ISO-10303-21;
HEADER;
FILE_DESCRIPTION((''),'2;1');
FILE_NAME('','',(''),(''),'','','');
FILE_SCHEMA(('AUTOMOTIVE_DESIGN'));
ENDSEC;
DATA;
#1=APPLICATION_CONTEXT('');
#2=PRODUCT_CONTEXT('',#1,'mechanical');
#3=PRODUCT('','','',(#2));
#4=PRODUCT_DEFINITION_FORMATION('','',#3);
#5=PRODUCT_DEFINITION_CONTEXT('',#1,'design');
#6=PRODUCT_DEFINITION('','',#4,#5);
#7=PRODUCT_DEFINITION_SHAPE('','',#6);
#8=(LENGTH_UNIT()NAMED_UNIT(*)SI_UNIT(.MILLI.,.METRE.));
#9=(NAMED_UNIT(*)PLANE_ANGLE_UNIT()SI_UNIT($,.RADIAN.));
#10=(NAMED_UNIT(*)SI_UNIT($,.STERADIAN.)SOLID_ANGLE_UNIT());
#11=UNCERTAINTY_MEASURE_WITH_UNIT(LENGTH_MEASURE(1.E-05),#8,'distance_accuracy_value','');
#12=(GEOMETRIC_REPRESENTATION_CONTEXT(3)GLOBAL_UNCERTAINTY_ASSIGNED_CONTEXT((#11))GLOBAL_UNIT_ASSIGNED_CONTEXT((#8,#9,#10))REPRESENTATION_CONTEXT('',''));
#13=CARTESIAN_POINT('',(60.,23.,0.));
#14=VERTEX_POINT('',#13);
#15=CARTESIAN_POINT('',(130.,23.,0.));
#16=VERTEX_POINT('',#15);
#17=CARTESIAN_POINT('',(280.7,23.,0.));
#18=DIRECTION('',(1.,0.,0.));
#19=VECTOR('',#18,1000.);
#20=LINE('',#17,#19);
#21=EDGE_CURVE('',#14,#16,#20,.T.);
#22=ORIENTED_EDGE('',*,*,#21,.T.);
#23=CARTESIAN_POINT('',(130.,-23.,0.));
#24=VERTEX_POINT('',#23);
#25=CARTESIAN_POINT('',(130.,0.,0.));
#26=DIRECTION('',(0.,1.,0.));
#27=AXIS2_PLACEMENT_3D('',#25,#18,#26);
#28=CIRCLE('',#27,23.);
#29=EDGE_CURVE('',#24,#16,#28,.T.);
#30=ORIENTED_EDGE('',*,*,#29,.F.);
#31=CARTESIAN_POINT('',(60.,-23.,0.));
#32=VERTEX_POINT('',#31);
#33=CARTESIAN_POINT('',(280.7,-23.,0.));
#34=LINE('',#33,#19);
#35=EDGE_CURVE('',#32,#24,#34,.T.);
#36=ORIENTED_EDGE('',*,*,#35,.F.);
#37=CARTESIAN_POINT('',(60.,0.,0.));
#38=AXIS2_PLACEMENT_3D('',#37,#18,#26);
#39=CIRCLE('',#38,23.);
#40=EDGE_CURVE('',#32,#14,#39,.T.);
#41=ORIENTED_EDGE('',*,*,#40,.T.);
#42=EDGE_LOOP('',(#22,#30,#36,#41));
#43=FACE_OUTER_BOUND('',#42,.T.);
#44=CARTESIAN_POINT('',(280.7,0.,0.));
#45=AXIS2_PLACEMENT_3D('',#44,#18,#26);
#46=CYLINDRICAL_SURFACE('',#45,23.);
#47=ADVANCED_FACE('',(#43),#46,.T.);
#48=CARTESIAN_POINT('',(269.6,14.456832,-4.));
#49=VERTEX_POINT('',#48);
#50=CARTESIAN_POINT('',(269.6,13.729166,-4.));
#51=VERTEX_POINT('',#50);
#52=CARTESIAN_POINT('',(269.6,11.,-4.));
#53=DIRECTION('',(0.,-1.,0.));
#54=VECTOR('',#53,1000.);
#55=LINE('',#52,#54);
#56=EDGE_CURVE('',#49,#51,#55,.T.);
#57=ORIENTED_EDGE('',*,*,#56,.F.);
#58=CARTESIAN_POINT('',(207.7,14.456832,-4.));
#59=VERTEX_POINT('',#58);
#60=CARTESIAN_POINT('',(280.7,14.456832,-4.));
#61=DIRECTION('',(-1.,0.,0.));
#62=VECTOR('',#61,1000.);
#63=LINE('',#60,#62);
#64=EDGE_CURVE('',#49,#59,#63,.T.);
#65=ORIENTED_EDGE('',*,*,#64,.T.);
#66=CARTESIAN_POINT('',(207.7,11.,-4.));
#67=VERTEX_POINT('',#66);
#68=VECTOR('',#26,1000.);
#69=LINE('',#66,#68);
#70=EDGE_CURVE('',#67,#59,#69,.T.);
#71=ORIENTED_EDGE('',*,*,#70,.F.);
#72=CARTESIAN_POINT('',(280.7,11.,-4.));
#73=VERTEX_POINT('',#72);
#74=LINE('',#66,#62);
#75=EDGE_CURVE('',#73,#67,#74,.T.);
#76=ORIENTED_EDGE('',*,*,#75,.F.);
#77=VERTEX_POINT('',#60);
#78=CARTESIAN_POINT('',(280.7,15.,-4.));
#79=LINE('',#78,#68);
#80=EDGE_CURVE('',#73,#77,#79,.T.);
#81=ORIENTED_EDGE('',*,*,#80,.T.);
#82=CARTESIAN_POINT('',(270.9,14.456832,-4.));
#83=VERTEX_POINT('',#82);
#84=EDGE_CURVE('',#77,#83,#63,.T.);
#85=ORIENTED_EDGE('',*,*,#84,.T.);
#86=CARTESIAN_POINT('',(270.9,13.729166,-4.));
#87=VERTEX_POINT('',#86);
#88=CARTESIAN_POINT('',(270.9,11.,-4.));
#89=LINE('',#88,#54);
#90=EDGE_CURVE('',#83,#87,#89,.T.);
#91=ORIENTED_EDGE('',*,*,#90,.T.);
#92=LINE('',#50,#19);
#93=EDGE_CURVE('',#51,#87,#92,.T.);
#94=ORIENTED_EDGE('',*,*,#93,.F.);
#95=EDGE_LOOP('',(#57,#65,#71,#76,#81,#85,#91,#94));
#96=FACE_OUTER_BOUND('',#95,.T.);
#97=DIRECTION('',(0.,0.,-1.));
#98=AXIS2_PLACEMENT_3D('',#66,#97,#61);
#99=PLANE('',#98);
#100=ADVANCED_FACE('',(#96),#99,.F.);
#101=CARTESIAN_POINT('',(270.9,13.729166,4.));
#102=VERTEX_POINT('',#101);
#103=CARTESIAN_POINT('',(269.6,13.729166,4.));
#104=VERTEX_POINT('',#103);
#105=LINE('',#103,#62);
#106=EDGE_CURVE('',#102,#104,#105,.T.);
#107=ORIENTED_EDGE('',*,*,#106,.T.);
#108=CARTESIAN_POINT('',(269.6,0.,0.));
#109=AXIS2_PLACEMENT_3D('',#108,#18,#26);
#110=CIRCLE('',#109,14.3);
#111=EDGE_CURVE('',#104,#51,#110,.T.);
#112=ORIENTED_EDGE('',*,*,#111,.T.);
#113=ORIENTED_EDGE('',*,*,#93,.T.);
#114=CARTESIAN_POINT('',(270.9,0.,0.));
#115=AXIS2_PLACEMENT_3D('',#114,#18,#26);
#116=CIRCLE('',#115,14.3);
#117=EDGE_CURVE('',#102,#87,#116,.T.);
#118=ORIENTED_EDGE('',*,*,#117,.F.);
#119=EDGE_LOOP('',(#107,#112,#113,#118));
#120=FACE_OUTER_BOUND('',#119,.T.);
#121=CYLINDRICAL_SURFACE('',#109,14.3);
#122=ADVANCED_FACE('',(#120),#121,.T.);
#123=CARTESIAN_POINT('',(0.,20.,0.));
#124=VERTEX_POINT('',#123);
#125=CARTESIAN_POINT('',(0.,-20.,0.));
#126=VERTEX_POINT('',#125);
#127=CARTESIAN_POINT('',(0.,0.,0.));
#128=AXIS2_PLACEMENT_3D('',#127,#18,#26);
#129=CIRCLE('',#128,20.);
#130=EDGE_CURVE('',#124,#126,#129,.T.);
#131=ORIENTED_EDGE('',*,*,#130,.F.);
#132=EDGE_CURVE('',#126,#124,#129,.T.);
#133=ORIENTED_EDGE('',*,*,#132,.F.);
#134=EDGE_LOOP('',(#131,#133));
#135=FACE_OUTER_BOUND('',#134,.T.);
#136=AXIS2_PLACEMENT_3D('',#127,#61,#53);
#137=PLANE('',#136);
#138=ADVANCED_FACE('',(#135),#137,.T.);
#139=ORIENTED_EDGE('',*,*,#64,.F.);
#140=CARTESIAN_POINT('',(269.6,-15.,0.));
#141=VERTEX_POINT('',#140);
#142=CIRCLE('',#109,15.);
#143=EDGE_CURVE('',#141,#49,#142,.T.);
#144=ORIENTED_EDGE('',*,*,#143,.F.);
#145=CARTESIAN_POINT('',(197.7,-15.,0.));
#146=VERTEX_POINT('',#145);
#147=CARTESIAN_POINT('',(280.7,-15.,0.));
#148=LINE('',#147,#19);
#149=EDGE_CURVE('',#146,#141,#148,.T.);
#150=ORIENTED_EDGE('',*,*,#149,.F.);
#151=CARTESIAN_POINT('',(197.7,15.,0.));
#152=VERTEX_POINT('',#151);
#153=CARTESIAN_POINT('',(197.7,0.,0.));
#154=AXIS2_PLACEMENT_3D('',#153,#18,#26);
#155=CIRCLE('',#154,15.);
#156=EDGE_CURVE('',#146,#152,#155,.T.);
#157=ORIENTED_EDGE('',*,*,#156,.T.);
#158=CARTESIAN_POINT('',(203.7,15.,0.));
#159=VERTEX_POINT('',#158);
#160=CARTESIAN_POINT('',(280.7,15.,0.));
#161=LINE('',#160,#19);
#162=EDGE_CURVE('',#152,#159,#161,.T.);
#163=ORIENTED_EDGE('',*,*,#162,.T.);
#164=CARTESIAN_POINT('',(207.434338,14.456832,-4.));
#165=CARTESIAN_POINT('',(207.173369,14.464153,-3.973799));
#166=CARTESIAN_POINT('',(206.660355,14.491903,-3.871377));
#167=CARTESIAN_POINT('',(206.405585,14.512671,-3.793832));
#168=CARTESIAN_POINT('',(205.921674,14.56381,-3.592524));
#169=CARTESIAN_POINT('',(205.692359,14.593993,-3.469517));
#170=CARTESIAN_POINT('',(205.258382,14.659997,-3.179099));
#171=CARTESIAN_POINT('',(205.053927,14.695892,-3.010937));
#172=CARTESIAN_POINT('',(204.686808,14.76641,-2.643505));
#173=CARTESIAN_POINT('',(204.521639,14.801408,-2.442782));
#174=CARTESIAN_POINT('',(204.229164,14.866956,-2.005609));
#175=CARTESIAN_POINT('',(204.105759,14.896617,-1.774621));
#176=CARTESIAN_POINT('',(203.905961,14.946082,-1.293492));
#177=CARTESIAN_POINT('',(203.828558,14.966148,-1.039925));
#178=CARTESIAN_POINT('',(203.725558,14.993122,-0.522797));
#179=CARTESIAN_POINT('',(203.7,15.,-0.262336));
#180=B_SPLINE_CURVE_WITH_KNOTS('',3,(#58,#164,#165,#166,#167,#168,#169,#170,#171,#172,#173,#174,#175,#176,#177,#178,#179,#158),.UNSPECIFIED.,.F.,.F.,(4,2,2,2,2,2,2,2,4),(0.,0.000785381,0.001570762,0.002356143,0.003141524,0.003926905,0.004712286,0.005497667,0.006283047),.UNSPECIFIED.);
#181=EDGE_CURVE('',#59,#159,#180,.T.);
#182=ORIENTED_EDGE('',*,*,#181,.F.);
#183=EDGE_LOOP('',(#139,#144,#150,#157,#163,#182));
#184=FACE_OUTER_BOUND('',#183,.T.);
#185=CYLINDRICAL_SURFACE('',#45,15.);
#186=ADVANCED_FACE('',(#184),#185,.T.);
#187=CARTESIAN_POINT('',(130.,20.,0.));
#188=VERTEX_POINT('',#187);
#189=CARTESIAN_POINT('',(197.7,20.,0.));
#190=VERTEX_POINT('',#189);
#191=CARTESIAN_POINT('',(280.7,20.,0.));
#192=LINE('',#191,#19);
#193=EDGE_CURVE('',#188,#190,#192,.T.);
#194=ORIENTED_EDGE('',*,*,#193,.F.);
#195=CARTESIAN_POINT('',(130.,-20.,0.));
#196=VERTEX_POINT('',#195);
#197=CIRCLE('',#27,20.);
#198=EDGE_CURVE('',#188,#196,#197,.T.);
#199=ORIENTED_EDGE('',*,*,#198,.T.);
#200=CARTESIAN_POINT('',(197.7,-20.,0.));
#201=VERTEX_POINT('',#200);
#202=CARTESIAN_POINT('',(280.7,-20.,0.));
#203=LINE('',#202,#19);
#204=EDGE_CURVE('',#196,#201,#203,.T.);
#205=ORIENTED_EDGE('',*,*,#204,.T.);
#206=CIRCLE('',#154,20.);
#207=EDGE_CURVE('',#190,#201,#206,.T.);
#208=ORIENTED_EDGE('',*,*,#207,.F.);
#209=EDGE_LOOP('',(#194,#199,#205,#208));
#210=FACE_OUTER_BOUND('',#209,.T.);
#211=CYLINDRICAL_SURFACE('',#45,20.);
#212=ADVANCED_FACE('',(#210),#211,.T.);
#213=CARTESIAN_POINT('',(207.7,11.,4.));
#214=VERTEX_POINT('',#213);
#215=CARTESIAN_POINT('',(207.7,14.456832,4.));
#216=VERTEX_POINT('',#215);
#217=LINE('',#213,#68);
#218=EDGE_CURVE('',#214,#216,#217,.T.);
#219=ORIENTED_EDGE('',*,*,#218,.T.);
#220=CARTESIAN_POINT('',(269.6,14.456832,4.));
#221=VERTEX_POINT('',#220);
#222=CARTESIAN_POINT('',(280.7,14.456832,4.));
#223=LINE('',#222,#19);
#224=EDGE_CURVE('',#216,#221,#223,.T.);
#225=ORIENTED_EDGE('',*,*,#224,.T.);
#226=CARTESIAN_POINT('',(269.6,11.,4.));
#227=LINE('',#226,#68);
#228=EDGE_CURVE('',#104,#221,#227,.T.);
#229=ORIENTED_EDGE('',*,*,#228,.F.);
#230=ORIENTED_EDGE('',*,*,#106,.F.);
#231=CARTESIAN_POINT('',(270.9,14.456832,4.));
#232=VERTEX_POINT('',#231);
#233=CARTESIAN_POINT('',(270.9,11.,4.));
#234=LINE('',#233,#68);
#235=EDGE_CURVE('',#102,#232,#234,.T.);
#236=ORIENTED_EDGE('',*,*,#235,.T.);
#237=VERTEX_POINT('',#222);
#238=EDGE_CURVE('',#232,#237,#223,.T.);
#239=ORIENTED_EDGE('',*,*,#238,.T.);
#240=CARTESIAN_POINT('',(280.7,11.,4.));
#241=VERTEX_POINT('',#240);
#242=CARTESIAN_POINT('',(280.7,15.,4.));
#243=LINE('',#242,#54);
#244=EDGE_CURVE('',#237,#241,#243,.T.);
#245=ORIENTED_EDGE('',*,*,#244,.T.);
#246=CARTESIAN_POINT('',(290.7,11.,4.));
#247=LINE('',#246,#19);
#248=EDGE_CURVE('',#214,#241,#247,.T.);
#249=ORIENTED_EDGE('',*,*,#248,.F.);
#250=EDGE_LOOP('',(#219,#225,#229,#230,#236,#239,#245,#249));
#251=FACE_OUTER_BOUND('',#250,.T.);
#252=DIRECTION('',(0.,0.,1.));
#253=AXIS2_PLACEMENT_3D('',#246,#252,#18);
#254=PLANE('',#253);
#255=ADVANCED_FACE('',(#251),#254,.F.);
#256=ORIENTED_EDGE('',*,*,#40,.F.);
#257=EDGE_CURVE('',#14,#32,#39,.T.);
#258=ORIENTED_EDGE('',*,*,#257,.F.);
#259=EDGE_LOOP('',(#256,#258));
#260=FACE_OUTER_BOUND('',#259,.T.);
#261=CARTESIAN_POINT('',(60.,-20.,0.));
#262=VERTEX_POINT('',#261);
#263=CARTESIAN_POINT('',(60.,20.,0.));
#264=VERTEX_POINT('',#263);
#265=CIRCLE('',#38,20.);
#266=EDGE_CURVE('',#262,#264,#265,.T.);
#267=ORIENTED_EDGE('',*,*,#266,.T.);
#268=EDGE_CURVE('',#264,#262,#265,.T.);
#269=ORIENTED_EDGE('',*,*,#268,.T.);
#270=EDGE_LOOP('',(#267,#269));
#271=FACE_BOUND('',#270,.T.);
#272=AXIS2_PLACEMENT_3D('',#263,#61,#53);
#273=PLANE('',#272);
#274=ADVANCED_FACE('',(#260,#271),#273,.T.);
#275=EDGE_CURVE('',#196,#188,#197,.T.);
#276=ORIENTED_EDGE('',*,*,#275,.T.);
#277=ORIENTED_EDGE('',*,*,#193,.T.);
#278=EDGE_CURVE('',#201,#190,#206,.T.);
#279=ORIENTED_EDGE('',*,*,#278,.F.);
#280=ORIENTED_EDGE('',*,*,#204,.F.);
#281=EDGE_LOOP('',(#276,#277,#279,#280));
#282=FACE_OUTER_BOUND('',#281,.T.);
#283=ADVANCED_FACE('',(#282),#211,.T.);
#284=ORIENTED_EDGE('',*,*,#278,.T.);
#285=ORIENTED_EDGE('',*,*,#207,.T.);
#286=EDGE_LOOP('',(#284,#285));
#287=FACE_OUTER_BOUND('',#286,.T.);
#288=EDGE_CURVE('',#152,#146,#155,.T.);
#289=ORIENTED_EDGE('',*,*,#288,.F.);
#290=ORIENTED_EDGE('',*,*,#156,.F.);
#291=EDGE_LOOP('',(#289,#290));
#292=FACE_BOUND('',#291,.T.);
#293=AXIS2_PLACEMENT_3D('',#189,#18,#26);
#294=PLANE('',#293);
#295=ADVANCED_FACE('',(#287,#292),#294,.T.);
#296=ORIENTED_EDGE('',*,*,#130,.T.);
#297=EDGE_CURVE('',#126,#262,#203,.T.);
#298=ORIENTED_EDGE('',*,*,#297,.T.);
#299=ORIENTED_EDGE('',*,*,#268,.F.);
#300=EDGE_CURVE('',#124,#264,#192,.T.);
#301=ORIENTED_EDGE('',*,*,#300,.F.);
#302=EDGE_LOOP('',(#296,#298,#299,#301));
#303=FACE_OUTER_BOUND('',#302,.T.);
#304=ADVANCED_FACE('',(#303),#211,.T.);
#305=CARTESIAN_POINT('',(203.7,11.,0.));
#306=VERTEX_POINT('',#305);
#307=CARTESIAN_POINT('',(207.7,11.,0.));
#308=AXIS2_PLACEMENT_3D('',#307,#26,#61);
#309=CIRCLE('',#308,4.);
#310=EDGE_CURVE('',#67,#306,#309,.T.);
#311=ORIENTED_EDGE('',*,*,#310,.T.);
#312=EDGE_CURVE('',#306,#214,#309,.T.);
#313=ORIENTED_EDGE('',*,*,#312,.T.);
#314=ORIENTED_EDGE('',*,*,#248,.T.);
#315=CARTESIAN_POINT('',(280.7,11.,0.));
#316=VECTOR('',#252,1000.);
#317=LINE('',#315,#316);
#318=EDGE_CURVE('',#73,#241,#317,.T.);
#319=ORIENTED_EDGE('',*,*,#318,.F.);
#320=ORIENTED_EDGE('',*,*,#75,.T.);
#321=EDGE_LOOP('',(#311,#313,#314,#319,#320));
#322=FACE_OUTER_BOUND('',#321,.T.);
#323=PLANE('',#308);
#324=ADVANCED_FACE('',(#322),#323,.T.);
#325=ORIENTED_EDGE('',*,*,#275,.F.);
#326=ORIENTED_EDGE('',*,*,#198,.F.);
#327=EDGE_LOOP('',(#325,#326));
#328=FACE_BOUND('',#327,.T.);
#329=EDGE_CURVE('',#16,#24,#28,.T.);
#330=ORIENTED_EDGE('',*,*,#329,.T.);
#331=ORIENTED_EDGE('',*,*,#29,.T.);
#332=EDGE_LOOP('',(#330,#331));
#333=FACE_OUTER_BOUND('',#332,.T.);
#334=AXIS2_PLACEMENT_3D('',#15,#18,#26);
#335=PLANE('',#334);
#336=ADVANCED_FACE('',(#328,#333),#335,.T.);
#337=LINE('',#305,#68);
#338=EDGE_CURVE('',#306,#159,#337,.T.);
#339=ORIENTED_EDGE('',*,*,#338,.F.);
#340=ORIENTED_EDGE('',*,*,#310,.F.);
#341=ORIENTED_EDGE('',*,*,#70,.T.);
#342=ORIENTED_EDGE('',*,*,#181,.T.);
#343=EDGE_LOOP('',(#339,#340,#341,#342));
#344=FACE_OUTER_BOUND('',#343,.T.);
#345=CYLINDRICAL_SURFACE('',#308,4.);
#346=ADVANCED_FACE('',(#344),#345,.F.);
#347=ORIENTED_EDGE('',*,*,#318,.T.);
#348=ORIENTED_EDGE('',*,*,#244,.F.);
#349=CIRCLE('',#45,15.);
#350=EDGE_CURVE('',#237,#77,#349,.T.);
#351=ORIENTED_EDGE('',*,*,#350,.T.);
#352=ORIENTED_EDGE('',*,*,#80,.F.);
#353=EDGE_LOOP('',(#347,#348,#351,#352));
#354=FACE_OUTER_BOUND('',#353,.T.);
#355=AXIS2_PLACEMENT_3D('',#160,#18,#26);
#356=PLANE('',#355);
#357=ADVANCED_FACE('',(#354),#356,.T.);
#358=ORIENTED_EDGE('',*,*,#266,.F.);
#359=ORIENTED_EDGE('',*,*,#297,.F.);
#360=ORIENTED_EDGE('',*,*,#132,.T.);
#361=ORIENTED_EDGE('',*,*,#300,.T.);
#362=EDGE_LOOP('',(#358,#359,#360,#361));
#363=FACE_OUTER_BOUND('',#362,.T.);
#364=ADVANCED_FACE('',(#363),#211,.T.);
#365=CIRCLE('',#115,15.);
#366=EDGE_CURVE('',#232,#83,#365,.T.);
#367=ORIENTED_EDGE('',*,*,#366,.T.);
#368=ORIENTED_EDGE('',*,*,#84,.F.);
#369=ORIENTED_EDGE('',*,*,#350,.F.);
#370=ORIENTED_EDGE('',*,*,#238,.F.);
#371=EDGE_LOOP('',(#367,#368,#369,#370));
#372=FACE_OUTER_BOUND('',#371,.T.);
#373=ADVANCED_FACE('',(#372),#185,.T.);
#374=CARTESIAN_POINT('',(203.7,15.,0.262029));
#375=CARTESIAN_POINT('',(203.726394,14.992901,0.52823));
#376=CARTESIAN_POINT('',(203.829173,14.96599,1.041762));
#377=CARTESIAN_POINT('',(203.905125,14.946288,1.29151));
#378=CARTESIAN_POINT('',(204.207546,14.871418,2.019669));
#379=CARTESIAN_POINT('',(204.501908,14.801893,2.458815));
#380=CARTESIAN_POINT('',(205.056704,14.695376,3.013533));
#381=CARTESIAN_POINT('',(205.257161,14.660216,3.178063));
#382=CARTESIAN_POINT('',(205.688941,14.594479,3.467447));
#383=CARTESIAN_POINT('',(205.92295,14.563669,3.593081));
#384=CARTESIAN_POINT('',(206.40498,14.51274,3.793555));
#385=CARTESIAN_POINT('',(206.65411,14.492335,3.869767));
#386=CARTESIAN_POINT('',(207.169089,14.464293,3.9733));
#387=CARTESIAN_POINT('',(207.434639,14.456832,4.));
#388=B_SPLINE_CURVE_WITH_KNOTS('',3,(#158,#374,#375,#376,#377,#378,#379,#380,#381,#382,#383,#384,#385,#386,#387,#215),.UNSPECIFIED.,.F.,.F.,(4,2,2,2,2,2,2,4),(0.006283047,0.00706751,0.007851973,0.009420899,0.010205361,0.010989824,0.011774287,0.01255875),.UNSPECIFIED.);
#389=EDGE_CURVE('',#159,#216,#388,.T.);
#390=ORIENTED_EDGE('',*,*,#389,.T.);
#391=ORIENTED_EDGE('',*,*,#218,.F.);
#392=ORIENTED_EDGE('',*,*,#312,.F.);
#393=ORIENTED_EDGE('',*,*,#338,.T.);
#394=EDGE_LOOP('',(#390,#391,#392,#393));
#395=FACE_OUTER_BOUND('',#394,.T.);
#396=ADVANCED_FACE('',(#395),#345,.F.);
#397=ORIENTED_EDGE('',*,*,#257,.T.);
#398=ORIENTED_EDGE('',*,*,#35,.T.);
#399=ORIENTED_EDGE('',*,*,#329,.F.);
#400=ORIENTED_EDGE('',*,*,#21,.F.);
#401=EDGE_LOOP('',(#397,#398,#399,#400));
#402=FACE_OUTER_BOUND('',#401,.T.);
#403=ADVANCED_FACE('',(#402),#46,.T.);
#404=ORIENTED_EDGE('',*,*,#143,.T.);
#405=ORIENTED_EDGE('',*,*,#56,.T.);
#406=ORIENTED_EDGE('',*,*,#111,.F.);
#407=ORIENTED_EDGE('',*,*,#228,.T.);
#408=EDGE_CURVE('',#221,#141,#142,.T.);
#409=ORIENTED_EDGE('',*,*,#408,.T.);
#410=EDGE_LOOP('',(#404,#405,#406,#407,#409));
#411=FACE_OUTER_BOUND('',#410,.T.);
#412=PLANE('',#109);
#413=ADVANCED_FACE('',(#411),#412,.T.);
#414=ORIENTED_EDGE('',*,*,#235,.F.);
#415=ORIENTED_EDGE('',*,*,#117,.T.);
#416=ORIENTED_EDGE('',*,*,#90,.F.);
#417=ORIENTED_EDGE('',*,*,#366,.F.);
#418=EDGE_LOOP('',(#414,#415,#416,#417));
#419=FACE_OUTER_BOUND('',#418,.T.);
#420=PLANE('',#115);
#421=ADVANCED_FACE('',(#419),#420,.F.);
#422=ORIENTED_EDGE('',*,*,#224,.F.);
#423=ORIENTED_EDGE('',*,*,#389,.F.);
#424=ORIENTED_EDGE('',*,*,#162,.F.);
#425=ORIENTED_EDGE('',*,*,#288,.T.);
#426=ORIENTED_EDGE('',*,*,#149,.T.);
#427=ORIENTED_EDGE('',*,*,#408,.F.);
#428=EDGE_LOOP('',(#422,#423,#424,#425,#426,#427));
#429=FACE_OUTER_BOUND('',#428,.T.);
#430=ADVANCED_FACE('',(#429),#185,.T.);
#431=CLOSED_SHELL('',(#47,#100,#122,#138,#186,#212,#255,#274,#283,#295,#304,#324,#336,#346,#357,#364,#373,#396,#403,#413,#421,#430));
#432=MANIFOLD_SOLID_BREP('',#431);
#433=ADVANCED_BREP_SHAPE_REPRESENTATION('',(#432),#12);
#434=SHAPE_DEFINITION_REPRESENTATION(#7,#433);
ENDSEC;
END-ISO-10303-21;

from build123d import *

# Parameters (mm, degrees)
CUT_EXTRUDE_1_DEPTH = 4
SKETCH_3_R          = 15
SKETCH_3_R_2        = 14.3
CUT_EXTRUDE_2_DEPTH = 1.3


with BuildPart() as part:
    # 草图1 → 旋转1 (revolve)
    with BuildSketch(Plane.XY):
        Polygon((0, 0), (0, 20), (60, 20), (60, 23), (130, 23), (130, 20), (197.7, 20), (197.7, 15), (280.7, 15), (280.7, 0), align=None)
    revolve(axis=Axis((280.7, 0, 0), (-1, 0, 0)))

    # 草图2 → 切除-拉伸1 (cut)
    with BuildSketch(Plane(origin=(0, 15, 0), x_dir=(1, 0, 0), z_dir=(0, 1, 0))):
        with BuildLine():
            Line((207.7, 4), (290.7, 4))
            Line((290.7, 4), (290.7, -4))
            Line((290.7, -4), (207.7, -4))
            ThreePointArc((207.7, -4), (203.7, 0), (207.7, 4))
        make_face()
    extrude(amount=-CUT_EXTRUDE_1_DEPTH, mode=Mode.SUBTRACT)

    # 草图3 → 切除-拉伸2 (cut)
    with BuildSketch(Plane(origin=(270.9, 0, 0), x_dir=(0, 0, -1), z_dir=(1, 0, 0))):
        with Locations(Location((0, 0, 0), (0, 0, 90))):
            Circle(SKETCH_3_R)
        Circle(SKETCH_3_R_2, mode=Mode.SUBTRACT)
    extrude(amount=-CUT_EXTRUDE_2_DEPTH, mode=Mode.SUBTRACT)


solid = part.part
